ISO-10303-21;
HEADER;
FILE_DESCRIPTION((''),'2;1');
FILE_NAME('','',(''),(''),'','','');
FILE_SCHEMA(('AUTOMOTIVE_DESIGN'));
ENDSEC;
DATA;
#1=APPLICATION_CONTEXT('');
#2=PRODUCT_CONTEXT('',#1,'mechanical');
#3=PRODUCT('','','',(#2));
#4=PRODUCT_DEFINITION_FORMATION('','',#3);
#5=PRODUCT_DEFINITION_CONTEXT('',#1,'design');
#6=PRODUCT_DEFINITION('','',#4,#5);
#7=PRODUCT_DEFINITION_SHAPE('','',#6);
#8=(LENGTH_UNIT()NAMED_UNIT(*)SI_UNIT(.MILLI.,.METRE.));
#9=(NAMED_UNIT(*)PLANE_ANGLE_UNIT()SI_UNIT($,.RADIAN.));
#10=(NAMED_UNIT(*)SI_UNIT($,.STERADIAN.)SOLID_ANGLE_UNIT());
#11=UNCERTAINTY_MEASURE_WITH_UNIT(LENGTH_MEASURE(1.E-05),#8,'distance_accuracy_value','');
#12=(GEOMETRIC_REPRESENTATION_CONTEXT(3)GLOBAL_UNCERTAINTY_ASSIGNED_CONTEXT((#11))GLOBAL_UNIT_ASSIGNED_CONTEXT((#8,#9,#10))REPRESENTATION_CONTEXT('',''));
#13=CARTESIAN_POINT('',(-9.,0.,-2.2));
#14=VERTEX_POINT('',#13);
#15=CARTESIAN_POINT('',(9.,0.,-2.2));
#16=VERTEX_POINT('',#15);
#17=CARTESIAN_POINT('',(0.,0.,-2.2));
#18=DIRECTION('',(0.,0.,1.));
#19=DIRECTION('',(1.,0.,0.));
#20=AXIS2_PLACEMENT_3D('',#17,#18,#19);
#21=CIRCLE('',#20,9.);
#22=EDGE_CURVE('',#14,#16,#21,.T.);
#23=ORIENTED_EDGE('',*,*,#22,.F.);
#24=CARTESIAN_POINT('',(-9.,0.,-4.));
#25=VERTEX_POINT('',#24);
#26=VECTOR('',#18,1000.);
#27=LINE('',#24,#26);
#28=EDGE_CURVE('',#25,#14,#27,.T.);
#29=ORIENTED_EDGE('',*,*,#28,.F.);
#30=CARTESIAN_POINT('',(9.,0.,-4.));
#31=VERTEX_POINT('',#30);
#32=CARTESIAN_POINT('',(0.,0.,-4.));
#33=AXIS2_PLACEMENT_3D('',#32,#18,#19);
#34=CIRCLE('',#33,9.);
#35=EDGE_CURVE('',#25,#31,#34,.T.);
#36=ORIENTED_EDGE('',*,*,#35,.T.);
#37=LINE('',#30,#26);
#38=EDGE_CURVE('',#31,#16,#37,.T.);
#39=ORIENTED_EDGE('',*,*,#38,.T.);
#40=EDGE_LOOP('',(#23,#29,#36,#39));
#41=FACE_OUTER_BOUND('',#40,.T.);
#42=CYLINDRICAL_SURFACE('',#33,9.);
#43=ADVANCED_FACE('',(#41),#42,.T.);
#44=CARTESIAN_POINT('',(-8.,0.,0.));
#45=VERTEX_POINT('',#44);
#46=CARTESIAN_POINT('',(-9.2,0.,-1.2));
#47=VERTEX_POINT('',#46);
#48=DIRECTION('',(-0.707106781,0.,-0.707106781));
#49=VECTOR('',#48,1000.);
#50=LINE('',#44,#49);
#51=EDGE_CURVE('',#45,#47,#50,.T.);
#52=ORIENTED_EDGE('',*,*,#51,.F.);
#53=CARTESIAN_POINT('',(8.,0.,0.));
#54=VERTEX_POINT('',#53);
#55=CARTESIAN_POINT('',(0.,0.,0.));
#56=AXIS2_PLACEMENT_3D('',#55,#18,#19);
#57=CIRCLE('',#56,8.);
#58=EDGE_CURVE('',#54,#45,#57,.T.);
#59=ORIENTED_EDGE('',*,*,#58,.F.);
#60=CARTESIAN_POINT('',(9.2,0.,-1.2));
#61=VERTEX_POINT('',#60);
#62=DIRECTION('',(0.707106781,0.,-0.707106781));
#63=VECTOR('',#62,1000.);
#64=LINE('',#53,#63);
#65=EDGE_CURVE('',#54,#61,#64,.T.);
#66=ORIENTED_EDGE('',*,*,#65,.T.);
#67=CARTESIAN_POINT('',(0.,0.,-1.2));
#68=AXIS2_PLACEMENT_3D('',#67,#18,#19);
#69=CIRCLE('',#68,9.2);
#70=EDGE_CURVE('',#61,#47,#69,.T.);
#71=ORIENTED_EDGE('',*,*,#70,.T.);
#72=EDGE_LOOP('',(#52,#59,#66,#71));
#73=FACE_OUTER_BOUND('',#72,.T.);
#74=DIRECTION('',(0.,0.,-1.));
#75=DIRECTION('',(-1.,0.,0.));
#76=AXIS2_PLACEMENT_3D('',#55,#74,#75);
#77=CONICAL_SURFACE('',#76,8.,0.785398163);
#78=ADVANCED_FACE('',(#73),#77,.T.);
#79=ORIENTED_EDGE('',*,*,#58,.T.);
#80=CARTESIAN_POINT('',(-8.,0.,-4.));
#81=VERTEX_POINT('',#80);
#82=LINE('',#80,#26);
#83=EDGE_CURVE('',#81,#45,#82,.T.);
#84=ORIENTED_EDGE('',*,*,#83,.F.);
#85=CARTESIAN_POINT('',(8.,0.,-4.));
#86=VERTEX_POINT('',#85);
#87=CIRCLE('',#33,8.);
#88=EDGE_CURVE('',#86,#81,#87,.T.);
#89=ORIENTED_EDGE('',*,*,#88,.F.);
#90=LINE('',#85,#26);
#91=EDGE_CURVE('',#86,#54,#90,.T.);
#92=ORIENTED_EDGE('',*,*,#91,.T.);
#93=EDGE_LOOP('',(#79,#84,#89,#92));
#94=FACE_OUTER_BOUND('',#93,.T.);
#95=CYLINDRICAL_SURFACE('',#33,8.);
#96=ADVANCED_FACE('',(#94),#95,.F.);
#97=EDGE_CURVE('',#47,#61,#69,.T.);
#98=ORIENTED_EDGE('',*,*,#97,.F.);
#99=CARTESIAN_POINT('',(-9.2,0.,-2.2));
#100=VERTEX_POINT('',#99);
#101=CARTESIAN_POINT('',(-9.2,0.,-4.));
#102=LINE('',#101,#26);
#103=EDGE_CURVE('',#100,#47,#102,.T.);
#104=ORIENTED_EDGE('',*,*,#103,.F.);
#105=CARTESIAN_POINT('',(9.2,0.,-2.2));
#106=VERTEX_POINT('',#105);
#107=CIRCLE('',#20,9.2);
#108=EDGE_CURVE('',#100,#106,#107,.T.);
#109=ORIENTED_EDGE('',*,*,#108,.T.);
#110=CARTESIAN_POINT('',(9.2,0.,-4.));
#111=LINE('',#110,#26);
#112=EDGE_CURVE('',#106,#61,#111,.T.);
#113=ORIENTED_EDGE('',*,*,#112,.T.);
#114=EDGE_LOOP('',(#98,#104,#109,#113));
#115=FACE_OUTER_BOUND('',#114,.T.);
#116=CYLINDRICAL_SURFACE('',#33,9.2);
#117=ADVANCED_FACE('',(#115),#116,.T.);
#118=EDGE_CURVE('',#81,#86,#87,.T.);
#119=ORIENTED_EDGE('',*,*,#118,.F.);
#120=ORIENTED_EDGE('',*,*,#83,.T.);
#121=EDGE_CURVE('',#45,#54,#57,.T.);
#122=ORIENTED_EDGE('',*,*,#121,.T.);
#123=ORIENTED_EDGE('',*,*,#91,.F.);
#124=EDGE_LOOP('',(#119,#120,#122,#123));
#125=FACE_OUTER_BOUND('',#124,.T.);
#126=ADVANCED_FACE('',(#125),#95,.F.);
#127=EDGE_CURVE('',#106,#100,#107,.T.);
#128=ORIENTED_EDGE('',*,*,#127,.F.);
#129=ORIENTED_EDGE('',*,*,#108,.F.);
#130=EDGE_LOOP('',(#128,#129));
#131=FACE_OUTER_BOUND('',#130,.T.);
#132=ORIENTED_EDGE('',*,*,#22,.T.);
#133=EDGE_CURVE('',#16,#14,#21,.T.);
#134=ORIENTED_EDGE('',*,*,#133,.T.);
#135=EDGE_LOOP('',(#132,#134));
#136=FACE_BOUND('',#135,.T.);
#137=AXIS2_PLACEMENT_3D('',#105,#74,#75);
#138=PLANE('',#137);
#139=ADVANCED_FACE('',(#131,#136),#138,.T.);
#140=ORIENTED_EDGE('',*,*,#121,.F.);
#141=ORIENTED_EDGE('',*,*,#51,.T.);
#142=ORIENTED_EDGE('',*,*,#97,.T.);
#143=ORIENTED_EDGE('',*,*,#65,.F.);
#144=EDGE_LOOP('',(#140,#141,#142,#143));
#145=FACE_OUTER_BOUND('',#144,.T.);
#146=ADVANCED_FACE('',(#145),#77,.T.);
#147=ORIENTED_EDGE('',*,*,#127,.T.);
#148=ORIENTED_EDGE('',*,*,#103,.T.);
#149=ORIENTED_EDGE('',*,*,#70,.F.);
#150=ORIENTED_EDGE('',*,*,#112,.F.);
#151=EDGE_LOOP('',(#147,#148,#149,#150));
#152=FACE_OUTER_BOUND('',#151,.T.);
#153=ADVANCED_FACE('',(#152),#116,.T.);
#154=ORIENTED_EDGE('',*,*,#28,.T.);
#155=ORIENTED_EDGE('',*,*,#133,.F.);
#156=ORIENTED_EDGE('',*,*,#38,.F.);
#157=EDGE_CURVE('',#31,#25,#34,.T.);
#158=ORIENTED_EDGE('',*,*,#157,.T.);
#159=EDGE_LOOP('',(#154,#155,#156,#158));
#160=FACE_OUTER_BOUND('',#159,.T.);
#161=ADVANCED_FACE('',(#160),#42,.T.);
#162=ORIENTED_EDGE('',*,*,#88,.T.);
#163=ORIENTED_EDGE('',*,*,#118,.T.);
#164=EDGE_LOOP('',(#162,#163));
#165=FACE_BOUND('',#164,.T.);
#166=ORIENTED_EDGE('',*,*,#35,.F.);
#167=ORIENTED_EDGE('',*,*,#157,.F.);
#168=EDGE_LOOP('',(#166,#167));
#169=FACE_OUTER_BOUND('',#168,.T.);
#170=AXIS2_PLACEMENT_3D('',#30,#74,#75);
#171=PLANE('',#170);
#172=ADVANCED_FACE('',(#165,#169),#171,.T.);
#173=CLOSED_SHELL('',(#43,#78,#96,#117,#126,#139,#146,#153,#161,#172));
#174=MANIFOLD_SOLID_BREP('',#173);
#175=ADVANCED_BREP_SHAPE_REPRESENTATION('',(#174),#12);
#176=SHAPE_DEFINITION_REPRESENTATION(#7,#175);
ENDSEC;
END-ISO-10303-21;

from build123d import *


with BuildPart() as part:
    # Sketch1 → Revolve1 (revolve)
    with BuildSketch(Plane(origin=(0, 0, 0), x_dir=(1, 0, 0), z_dir=(0, 1, 0))):
        Polygon((8, 4), (8, 0), (9.2, 1.2), (9.2, 2.2), (9, 2.2), (9, 4), align=None)
    revolve(axis=Axis((0, 0, -4), (0, 0, 1)))


solid = part.part
